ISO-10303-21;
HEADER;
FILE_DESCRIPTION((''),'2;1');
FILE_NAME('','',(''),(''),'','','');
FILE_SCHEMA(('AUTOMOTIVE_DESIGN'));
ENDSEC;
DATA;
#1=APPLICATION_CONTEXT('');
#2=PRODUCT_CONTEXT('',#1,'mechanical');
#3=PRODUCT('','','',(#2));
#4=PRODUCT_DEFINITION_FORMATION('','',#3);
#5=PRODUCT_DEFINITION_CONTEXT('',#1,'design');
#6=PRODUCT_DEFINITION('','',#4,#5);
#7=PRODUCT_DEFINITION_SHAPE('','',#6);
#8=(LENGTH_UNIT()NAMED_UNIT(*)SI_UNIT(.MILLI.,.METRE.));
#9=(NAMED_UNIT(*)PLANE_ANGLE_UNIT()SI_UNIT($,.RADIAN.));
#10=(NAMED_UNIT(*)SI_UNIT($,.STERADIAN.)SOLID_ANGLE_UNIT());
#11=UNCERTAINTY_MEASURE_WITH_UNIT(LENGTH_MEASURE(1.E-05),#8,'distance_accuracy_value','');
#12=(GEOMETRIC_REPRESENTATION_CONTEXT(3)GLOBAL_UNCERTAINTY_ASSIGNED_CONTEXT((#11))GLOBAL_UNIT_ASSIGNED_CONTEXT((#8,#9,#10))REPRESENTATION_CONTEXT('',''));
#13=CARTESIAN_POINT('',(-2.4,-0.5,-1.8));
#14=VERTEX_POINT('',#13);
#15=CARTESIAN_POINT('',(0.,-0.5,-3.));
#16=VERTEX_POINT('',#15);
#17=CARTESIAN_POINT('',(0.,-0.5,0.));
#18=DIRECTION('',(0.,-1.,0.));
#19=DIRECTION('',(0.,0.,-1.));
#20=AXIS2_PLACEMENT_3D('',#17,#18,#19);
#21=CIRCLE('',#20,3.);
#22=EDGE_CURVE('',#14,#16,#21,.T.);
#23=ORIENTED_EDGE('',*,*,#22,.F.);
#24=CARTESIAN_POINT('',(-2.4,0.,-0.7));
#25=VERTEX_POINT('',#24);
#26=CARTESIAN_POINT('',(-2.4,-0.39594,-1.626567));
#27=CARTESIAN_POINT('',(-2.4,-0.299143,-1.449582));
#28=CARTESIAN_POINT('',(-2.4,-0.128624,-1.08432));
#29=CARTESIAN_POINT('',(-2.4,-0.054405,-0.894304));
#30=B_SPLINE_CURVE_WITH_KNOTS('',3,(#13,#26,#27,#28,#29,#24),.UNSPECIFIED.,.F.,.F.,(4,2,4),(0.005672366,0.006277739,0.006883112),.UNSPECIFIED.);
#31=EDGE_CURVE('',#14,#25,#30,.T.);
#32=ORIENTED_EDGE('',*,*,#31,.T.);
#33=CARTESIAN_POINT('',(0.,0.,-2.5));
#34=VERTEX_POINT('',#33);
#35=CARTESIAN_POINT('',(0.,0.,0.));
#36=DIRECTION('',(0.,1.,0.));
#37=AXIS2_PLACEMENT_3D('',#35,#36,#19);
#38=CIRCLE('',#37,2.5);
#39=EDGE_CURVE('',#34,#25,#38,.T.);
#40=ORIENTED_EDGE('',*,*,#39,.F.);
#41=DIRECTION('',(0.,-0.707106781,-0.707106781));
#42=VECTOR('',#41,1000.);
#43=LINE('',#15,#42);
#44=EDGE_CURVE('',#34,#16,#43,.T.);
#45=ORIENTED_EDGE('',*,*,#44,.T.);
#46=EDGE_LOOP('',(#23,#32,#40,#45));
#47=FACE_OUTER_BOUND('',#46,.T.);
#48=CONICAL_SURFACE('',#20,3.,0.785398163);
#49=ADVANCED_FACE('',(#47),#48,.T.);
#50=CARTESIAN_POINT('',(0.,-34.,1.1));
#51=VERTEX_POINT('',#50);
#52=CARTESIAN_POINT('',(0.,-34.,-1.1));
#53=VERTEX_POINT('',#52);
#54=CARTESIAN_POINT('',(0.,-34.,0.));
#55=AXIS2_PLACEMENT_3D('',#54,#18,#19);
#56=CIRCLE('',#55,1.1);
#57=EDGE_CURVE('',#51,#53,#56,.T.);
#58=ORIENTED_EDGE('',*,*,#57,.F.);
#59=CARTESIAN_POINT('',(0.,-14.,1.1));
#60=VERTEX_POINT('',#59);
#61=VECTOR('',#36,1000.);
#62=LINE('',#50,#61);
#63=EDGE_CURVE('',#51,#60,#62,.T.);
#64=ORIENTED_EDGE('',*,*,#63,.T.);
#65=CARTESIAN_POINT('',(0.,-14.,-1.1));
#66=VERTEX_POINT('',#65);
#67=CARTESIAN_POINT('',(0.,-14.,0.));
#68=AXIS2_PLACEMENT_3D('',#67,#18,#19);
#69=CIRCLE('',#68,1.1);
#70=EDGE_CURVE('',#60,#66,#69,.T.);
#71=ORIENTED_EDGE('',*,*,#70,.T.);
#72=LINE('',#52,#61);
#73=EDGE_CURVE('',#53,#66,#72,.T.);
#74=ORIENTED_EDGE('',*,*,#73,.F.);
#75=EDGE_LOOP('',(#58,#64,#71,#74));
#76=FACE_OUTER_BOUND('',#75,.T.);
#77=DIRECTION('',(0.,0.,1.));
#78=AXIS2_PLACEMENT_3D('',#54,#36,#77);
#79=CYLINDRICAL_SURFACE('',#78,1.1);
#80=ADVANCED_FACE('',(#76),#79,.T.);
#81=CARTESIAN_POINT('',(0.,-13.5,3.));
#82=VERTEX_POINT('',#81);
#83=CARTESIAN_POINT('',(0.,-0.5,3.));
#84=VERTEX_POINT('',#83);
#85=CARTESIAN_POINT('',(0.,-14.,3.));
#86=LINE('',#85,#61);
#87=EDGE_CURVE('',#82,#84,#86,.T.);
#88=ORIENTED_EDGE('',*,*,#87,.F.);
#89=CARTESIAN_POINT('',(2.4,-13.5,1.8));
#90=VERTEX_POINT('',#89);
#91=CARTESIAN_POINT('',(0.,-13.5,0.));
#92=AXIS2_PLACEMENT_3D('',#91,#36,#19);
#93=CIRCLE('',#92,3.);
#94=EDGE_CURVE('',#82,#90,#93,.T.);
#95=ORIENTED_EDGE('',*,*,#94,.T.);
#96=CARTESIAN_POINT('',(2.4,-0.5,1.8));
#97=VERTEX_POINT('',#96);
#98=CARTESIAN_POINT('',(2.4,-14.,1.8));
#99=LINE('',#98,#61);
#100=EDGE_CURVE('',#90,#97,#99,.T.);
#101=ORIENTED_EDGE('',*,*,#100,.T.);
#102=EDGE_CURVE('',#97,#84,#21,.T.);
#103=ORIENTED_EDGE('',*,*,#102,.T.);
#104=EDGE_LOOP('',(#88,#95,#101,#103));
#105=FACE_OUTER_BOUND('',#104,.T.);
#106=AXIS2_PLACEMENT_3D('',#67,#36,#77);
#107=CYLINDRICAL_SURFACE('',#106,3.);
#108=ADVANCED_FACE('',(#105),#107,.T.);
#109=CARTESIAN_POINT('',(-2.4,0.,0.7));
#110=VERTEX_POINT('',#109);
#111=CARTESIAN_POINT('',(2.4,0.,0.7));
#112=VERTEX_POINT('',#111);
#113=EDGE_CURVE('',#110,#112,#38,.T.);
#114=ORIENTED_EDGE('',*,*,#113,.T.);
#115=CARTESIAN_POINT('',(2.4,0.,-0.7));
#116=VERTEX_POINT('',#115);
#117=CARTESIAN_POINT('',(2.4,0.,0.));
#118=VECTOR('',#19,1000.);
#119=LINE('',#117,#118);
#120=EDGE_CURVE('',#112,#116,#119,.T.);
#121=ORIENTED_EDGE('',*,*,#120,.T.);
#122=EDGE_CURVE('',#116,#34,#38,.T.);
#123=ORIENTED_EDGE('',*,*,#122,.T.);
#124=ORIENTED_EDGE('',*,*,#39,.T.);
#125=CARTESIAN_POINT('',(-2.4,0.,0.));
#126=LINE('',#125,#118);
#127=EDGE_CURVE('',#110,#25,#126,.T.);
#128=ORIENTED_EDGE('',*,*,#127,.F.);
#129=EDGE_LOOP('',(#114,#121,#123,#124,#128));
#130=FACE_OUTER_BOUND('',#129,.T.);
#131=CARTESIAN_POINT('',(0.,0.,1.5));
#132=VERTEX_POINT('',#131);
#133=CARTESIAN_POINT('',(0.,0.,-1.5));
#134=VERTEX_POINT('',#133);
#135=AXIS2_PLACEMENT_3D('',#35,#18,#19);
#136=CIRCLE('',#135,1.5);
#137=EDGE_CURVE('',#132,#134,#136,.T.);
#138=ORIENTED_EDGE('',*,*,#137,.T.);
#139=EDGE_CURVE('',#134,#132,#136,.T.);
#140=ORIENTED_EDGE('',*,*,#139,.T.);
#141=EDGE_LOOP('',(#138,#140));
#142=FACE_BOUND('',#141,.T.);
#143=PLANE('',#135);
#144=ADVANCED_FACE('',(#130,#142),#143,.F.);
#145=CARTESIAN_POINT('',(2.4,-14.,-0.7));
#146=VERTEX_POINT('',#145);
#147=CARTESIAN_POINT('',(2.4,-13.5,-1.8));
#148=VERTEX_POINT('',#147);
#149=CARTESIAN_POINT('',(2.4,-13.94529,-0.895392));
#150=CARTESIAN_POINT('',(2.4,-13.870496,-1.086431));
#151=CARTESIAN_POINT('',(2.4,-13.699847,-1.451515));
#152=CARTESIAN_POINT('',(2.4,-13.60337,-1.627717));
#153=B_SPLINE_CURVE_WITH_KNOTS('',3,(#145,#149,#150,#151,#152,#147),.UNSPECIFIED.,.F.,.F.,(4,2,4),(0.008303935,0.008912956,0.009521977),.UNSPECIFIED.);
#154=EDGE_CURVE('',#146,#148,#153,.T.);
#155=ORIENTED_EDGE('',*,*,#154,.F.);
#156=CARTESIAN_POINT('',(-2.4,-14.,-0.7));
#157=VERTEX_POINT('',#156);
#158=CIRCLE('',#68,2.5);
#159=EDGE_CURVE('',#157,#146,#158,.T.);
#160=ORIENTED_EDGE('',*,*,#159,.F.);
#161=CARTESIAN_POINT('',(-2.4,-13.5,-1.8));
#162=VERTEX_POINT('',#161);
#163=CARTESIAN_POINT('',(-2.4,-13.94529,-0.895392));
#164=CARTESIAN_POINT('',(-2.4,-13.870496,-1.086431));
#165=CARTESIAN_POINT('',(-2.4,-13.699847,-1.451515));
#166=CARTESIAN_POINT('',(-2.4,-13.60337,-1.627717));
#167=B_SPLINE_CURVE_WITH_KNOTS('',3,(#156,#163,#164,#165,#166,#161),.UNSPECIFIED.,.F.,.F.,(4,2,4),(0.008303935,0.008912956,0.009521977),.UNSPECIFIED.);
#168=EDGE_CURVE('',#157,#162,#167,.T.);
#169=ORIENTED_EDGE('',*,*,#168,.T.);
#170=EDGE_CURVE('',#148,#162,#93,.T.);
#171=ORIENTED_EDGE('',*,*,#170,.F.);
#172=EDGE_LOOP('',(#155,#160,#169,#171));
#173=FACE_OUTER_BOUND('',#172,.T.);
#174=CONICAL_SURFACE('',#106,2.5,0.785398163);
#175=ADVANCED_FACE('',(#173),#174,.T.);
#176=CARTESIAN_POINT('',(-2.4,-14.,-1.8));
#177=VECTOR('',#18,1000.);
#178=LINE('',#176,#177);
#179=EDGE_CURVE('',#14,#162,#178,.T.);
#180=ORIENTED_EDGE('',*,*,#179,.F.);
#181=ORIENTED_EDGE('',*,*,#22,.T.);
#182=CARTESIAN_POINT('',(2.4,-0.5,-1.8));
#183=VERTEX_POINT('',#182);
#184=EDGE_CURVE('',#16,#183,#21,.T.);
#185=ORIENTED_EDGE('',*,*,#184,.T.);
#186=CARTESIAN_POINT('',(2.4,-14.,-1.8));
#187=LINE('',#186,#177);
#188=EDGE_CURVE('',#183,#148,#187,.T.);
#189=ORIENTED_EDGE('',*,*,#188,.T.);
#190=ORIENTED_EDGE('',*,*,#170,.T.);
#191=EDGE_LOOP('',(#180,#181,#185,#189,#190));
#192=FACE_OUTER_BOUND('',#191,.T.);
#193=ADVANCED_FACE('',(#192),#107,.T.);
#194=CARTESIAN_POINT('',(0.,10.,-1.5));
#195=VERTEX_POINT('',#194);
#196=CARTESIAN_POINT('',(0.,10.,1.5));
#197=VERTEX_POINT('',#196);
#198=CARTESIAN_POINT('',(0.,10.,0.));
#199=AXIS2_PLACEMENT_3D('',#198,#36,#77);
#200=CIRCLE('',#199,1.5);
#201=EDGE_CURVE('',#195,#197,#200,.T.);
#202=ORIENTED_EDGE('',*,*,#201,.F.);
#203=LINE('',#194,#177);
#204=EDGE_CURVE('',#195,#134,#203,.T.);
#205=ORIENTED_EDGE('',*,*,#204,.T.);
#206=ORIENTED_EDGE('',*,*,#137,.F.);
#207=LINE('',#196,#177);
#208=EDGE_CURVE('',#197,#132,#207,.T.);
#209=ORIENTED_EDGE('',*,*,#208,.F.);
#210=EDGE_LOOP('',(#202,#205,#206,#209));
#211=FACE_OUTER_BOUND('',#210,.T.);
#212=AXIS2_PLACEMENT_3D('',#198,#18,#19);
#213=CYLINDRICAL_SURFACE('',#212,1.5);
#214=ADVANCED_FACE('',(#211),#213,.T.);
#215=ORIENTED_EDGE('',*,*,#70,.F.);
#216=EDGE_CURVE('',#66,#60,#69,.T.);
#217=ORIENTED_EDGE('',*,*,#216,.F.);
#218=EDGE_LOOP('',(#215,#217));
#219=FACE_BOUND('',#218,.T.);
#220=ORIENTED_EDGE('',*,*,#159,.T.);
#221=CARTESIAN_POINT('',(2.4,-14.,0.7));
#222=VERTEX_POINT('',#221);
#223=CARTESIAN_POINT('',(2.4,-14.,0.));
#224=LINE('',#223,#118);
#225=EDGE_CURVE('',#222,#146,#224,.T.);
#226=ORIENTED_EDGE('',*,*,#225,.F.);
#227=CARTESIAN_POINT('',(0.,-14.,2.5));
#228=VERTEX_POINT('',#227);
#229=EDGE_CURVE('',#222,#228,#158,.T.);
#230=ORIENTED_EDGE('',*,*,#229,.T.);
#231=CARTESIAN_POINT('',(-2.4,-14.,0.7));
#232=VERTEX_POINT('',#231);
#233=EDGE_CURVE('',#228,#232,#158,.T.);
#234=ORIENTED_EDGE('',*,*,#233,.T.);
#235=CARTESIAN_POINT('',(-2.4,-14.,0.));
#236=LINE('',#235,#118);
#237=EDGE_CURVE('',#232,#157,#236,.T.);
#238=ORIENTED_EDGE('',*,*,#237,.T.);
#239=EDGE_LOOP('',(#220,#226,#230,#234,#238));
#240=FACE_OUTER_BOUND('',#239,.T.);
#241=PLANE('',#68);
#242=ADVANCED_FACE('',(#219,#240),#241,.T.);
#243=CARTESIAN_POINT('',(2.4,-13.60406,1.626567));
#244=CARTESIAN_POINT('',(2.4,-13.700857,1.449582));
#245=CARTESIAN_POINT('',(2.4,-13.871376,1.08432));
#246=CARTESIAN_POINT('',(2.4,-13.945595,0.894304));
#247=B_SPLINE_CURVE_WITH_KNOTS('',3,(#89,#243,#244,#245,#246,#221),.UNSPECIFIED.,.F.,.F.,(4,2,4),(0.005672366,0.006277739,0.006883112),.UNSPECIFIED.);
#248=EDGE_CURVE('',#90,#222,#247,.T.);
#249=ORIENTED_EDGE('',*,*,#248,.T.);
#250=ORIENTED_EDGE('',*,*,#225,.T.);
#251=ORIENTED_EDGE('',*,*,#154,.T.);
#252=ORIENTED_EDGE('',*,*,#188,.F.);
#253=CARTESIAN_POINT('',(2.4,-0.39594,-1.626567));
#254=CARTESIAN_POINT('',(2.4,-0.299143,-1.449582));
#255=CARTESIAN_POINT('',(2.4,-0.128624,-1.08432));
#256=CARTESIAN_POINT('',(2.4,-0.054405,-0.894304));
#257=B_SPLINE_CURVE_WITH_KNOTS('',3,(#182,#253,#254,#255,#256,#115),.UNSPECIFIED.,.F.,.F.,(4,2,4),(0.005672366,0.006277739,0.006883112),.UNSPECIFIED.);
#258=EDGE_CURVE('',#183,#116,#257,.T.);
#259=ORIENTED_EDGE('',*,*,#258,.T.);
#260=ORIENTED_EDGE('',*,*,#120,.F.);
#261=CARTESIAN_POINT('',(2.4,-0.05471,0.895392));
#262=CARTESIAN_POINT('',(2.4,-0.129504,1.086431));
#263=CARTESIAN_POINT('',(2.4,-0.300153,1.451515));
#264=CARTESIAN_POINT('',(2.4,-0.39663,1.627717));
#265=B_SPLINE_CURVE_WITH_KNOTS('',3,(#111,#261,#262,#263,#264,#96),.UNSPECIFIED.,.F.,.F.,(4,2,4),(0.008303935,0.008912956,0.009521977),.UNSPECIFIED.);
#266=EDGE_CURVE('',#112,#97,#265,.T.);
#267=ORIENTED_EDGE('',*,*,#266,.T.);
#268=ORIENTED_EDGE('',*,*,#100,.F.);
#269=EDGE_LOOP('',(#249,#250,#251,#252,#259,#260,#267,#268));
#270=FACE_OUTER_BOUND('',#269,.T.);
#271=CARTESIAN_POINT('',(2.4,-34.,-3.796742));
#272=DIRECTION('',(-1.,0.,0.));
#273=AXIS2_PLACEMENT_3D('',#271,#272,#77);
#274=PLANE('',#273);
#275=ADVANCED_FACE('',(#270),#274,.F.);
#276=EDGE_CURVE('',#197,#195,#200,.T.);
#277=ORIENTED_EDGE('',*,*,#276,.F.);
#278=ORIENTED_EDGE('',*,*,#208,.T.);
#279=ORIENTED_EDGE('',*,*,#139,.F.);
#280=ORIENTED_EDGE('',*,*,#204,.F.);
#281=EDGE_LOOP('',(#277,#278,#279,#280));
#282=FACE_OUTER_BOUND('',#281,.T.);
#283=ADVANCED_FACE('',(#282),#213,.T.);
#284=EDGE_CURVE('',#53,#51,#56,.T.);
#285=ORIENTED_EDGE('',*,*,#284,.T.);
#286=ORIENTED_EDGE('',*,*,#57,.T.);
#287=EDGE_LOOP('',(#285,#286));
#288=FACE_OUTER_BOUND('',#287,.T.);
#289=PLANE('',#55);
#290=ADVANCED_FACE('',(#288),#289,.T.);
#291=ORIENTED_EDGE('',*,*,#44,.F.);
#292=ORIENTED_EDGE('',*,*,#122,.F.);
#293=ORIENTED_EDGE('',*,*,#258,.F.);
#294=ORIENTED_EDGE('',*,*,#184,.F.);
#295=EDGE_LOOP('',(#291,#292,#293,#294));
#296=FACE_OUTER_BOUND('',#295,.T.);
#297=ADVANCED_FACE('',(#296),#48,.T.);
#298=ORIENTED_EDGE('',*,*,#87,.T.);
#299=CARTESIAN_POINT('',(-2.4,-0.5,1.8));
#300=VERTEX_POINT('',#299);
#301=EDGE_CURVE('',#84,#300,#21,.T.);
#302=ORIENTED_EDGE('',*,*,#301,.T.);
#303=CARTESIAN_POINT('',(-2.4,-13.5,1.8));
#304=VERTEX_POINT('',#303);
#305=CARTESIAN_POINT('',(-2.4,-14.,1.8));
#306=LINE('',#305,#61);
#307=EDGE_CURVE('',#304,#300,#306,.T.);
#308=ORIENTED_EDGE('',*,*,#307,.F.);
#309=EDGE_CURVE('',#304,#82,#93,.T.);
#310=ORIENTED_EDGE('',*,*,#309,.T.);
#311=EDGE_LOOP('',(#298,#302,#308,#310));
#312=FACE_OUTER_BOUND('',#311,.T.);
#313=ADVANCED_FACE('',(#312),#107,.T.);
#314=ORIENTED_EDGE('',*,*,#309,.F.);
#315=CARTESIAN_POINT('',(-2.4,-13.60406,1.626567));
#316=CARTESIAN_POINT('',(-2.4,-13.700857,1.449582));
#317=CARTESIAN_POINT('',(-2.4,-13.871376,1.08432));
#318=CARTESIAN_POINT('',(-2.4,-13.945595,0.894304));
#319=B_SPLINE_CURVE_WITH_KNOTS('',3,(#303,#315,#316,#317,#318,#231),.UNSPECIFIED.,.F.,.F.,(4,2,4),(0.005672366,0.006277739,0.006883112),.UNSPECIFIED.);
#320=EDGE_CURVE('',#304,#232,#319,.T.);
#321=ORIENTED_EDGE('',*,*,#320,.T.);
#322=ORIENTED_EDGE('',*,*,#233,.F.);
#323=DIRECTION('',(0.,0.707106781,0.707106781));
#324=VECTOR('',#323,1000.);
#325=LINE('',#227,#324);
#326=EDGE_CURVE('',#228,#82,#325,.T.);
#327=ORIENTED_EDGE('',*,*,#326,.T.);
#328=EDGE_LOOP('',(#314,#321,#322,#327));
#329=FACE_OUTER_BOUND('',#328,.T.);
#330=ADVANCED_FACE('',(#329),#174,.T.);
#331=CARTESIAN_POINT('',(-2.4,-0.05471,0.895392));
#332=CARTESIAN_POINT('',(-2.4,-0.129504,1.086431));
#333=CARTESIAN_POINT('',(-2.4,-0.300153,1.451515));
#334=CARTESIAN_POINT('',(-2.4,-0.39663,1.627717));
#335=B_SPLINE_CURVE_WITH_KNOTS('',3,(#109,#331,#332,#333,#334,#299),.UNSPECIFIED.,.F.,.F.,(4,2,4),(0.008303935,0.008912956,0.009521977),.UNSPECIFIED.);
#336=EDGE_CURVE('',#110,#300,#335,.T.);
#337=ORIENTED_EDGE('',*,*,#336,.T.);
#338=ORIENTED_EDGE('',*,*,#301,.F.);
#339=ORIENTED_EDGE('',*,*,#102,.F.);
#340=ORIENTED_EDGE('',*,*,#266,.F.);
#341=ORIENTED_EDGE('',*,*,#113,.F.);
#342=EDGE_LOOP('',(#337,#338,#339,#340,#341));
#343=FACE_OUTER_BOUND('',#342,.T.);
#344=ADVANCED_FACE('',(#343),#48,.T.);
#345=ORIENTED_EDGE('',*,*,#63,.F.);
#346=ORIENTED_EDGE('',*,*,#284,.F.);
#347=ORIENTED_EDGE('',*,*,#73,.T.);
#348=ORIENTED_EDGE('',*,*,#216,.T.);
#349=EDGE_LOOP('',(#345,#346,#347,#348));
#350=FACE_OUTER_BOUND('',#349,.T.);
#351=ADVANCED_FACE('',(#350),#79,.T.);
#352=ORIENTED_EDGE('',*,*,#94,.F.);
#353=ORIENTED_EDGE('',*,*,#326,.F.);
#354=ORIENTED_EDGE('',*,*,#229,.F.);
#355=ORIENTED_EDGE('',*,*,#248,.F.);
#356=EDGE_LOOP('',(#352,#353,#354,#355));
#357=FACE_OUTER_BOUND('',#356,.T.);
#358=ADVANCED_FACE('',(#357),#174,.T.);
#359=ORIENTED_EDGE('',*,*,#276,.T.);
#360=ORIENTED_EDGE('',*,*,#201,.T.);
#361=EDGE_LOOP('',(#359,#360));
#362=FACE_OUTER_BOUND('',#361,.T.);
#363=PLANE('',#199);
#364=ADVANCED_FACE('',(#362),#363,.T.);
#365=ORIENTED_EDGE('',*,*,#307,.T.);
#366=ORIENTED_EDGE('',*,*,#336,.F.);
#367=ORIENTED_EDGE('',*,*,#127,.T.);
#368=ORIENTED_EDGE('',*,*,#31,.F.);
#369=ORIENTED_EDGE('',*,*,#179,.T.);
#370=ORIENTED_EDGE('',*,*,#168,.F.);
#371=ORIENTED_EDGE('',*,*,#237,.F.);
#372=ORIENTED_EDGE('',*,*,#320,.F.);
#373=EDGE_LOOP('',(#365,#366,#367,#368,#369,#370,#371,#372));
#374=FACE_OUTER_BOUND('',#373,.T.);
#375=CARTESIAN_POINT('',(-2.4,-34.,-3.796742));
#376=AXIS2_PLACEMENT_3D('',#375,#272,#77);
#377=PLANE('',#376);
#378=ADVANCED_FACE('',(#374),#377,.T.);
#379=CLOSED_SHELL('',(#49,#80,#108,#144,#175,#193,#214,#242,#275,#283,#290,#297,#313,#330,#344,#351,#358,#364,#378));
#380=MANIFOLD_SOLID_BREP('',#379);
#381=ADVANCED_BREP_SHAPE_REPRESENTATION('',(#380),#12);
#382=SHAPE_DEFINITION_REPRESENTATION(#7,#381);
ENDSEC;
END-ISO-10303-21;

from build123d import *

# Parameters (mm, degrees)
SKETCH_1_R          = 1.5
EXTRUDE_1_DEPTH     = 10
SKETCH_2_R          = 3
M6X0_75P_DEPTH      = 14
SKETCH_3_R          = 1.1
EXTRUDE_3_DEPTH     = 20
CHAMFER_1_SIZE      = 0.5
SKETCH_4_W          = 2.061421144
SKETCH_4_H          = 7.488665512
CUT_EXTRUDE_1_DEPTH = 45.204072211


with BuildPart() as part:
    # 草图1 → 凸台-拉伸1 (new body)
    with BuildSketch(Plane(origin=(0, 0, 0), x_dir=(1, 0, 0), z_dir=(0, 1, 0))):
        with Locations(Location((0, 0, 0), (0, 0, 270))):
            Circle(SKETCH_1_R)
    extrude(amount=EXTRUDE_1_DEPTH)

    # 草图2 → M6X0.75P (add)
    with BuildSketch(Plane.XZ):
        with Locations(Location((0, 0, 0), (0, 0, 270))):
            Circle(SKETCH_2_R)
    extrude(amount=M6X0_75P_DEPTH)

    # 草图3 → 凸台-拉伸3 (add)
    with BuildSketch(Plane.XZ.offset(14)):
        with Locations(Location((0, 0, 0), (0, 0, 270))):
            Circle(SKETCH_3_R)
    extrude(amount=EXTRUDE_3_DEPTH)

    # 倒角1
    chamfer_1_edges = [part.edges().sort_by_distance(p)[0] for p in [
        (0, 0, 3),
        (0, -14, 3),
    ]]
    chamfer(chamfer_1_edges, length=CHAMFER_1_SIZE)

    # 草图4 → 切除-拉伸1 (cut, through all)
    with BuildSketch(Plane(origin=(0, 10, 0), x_dir=(1, 0, 0), z_dir=(0, 1, 0))):
        with Locations((3.430710572, 0.052409012)):
            Rectangle(SKETCH_4_W, SKETCH_4_H)
    cut_extrude_1 = extrude(amount=-CUT_EXTRUDE_1_DEPTH, mode=Mode.SUBTRACT)

    # 镜向1: 切除-拉伸1 across plane
    add(cut_extrude_1.mirror(Plane(origin=(0, 0, 0), x_dir=(0, 0, 1), z_dir=(1, 0, 0))), mode=Mode.SUBTRACT)


solid = part.part
